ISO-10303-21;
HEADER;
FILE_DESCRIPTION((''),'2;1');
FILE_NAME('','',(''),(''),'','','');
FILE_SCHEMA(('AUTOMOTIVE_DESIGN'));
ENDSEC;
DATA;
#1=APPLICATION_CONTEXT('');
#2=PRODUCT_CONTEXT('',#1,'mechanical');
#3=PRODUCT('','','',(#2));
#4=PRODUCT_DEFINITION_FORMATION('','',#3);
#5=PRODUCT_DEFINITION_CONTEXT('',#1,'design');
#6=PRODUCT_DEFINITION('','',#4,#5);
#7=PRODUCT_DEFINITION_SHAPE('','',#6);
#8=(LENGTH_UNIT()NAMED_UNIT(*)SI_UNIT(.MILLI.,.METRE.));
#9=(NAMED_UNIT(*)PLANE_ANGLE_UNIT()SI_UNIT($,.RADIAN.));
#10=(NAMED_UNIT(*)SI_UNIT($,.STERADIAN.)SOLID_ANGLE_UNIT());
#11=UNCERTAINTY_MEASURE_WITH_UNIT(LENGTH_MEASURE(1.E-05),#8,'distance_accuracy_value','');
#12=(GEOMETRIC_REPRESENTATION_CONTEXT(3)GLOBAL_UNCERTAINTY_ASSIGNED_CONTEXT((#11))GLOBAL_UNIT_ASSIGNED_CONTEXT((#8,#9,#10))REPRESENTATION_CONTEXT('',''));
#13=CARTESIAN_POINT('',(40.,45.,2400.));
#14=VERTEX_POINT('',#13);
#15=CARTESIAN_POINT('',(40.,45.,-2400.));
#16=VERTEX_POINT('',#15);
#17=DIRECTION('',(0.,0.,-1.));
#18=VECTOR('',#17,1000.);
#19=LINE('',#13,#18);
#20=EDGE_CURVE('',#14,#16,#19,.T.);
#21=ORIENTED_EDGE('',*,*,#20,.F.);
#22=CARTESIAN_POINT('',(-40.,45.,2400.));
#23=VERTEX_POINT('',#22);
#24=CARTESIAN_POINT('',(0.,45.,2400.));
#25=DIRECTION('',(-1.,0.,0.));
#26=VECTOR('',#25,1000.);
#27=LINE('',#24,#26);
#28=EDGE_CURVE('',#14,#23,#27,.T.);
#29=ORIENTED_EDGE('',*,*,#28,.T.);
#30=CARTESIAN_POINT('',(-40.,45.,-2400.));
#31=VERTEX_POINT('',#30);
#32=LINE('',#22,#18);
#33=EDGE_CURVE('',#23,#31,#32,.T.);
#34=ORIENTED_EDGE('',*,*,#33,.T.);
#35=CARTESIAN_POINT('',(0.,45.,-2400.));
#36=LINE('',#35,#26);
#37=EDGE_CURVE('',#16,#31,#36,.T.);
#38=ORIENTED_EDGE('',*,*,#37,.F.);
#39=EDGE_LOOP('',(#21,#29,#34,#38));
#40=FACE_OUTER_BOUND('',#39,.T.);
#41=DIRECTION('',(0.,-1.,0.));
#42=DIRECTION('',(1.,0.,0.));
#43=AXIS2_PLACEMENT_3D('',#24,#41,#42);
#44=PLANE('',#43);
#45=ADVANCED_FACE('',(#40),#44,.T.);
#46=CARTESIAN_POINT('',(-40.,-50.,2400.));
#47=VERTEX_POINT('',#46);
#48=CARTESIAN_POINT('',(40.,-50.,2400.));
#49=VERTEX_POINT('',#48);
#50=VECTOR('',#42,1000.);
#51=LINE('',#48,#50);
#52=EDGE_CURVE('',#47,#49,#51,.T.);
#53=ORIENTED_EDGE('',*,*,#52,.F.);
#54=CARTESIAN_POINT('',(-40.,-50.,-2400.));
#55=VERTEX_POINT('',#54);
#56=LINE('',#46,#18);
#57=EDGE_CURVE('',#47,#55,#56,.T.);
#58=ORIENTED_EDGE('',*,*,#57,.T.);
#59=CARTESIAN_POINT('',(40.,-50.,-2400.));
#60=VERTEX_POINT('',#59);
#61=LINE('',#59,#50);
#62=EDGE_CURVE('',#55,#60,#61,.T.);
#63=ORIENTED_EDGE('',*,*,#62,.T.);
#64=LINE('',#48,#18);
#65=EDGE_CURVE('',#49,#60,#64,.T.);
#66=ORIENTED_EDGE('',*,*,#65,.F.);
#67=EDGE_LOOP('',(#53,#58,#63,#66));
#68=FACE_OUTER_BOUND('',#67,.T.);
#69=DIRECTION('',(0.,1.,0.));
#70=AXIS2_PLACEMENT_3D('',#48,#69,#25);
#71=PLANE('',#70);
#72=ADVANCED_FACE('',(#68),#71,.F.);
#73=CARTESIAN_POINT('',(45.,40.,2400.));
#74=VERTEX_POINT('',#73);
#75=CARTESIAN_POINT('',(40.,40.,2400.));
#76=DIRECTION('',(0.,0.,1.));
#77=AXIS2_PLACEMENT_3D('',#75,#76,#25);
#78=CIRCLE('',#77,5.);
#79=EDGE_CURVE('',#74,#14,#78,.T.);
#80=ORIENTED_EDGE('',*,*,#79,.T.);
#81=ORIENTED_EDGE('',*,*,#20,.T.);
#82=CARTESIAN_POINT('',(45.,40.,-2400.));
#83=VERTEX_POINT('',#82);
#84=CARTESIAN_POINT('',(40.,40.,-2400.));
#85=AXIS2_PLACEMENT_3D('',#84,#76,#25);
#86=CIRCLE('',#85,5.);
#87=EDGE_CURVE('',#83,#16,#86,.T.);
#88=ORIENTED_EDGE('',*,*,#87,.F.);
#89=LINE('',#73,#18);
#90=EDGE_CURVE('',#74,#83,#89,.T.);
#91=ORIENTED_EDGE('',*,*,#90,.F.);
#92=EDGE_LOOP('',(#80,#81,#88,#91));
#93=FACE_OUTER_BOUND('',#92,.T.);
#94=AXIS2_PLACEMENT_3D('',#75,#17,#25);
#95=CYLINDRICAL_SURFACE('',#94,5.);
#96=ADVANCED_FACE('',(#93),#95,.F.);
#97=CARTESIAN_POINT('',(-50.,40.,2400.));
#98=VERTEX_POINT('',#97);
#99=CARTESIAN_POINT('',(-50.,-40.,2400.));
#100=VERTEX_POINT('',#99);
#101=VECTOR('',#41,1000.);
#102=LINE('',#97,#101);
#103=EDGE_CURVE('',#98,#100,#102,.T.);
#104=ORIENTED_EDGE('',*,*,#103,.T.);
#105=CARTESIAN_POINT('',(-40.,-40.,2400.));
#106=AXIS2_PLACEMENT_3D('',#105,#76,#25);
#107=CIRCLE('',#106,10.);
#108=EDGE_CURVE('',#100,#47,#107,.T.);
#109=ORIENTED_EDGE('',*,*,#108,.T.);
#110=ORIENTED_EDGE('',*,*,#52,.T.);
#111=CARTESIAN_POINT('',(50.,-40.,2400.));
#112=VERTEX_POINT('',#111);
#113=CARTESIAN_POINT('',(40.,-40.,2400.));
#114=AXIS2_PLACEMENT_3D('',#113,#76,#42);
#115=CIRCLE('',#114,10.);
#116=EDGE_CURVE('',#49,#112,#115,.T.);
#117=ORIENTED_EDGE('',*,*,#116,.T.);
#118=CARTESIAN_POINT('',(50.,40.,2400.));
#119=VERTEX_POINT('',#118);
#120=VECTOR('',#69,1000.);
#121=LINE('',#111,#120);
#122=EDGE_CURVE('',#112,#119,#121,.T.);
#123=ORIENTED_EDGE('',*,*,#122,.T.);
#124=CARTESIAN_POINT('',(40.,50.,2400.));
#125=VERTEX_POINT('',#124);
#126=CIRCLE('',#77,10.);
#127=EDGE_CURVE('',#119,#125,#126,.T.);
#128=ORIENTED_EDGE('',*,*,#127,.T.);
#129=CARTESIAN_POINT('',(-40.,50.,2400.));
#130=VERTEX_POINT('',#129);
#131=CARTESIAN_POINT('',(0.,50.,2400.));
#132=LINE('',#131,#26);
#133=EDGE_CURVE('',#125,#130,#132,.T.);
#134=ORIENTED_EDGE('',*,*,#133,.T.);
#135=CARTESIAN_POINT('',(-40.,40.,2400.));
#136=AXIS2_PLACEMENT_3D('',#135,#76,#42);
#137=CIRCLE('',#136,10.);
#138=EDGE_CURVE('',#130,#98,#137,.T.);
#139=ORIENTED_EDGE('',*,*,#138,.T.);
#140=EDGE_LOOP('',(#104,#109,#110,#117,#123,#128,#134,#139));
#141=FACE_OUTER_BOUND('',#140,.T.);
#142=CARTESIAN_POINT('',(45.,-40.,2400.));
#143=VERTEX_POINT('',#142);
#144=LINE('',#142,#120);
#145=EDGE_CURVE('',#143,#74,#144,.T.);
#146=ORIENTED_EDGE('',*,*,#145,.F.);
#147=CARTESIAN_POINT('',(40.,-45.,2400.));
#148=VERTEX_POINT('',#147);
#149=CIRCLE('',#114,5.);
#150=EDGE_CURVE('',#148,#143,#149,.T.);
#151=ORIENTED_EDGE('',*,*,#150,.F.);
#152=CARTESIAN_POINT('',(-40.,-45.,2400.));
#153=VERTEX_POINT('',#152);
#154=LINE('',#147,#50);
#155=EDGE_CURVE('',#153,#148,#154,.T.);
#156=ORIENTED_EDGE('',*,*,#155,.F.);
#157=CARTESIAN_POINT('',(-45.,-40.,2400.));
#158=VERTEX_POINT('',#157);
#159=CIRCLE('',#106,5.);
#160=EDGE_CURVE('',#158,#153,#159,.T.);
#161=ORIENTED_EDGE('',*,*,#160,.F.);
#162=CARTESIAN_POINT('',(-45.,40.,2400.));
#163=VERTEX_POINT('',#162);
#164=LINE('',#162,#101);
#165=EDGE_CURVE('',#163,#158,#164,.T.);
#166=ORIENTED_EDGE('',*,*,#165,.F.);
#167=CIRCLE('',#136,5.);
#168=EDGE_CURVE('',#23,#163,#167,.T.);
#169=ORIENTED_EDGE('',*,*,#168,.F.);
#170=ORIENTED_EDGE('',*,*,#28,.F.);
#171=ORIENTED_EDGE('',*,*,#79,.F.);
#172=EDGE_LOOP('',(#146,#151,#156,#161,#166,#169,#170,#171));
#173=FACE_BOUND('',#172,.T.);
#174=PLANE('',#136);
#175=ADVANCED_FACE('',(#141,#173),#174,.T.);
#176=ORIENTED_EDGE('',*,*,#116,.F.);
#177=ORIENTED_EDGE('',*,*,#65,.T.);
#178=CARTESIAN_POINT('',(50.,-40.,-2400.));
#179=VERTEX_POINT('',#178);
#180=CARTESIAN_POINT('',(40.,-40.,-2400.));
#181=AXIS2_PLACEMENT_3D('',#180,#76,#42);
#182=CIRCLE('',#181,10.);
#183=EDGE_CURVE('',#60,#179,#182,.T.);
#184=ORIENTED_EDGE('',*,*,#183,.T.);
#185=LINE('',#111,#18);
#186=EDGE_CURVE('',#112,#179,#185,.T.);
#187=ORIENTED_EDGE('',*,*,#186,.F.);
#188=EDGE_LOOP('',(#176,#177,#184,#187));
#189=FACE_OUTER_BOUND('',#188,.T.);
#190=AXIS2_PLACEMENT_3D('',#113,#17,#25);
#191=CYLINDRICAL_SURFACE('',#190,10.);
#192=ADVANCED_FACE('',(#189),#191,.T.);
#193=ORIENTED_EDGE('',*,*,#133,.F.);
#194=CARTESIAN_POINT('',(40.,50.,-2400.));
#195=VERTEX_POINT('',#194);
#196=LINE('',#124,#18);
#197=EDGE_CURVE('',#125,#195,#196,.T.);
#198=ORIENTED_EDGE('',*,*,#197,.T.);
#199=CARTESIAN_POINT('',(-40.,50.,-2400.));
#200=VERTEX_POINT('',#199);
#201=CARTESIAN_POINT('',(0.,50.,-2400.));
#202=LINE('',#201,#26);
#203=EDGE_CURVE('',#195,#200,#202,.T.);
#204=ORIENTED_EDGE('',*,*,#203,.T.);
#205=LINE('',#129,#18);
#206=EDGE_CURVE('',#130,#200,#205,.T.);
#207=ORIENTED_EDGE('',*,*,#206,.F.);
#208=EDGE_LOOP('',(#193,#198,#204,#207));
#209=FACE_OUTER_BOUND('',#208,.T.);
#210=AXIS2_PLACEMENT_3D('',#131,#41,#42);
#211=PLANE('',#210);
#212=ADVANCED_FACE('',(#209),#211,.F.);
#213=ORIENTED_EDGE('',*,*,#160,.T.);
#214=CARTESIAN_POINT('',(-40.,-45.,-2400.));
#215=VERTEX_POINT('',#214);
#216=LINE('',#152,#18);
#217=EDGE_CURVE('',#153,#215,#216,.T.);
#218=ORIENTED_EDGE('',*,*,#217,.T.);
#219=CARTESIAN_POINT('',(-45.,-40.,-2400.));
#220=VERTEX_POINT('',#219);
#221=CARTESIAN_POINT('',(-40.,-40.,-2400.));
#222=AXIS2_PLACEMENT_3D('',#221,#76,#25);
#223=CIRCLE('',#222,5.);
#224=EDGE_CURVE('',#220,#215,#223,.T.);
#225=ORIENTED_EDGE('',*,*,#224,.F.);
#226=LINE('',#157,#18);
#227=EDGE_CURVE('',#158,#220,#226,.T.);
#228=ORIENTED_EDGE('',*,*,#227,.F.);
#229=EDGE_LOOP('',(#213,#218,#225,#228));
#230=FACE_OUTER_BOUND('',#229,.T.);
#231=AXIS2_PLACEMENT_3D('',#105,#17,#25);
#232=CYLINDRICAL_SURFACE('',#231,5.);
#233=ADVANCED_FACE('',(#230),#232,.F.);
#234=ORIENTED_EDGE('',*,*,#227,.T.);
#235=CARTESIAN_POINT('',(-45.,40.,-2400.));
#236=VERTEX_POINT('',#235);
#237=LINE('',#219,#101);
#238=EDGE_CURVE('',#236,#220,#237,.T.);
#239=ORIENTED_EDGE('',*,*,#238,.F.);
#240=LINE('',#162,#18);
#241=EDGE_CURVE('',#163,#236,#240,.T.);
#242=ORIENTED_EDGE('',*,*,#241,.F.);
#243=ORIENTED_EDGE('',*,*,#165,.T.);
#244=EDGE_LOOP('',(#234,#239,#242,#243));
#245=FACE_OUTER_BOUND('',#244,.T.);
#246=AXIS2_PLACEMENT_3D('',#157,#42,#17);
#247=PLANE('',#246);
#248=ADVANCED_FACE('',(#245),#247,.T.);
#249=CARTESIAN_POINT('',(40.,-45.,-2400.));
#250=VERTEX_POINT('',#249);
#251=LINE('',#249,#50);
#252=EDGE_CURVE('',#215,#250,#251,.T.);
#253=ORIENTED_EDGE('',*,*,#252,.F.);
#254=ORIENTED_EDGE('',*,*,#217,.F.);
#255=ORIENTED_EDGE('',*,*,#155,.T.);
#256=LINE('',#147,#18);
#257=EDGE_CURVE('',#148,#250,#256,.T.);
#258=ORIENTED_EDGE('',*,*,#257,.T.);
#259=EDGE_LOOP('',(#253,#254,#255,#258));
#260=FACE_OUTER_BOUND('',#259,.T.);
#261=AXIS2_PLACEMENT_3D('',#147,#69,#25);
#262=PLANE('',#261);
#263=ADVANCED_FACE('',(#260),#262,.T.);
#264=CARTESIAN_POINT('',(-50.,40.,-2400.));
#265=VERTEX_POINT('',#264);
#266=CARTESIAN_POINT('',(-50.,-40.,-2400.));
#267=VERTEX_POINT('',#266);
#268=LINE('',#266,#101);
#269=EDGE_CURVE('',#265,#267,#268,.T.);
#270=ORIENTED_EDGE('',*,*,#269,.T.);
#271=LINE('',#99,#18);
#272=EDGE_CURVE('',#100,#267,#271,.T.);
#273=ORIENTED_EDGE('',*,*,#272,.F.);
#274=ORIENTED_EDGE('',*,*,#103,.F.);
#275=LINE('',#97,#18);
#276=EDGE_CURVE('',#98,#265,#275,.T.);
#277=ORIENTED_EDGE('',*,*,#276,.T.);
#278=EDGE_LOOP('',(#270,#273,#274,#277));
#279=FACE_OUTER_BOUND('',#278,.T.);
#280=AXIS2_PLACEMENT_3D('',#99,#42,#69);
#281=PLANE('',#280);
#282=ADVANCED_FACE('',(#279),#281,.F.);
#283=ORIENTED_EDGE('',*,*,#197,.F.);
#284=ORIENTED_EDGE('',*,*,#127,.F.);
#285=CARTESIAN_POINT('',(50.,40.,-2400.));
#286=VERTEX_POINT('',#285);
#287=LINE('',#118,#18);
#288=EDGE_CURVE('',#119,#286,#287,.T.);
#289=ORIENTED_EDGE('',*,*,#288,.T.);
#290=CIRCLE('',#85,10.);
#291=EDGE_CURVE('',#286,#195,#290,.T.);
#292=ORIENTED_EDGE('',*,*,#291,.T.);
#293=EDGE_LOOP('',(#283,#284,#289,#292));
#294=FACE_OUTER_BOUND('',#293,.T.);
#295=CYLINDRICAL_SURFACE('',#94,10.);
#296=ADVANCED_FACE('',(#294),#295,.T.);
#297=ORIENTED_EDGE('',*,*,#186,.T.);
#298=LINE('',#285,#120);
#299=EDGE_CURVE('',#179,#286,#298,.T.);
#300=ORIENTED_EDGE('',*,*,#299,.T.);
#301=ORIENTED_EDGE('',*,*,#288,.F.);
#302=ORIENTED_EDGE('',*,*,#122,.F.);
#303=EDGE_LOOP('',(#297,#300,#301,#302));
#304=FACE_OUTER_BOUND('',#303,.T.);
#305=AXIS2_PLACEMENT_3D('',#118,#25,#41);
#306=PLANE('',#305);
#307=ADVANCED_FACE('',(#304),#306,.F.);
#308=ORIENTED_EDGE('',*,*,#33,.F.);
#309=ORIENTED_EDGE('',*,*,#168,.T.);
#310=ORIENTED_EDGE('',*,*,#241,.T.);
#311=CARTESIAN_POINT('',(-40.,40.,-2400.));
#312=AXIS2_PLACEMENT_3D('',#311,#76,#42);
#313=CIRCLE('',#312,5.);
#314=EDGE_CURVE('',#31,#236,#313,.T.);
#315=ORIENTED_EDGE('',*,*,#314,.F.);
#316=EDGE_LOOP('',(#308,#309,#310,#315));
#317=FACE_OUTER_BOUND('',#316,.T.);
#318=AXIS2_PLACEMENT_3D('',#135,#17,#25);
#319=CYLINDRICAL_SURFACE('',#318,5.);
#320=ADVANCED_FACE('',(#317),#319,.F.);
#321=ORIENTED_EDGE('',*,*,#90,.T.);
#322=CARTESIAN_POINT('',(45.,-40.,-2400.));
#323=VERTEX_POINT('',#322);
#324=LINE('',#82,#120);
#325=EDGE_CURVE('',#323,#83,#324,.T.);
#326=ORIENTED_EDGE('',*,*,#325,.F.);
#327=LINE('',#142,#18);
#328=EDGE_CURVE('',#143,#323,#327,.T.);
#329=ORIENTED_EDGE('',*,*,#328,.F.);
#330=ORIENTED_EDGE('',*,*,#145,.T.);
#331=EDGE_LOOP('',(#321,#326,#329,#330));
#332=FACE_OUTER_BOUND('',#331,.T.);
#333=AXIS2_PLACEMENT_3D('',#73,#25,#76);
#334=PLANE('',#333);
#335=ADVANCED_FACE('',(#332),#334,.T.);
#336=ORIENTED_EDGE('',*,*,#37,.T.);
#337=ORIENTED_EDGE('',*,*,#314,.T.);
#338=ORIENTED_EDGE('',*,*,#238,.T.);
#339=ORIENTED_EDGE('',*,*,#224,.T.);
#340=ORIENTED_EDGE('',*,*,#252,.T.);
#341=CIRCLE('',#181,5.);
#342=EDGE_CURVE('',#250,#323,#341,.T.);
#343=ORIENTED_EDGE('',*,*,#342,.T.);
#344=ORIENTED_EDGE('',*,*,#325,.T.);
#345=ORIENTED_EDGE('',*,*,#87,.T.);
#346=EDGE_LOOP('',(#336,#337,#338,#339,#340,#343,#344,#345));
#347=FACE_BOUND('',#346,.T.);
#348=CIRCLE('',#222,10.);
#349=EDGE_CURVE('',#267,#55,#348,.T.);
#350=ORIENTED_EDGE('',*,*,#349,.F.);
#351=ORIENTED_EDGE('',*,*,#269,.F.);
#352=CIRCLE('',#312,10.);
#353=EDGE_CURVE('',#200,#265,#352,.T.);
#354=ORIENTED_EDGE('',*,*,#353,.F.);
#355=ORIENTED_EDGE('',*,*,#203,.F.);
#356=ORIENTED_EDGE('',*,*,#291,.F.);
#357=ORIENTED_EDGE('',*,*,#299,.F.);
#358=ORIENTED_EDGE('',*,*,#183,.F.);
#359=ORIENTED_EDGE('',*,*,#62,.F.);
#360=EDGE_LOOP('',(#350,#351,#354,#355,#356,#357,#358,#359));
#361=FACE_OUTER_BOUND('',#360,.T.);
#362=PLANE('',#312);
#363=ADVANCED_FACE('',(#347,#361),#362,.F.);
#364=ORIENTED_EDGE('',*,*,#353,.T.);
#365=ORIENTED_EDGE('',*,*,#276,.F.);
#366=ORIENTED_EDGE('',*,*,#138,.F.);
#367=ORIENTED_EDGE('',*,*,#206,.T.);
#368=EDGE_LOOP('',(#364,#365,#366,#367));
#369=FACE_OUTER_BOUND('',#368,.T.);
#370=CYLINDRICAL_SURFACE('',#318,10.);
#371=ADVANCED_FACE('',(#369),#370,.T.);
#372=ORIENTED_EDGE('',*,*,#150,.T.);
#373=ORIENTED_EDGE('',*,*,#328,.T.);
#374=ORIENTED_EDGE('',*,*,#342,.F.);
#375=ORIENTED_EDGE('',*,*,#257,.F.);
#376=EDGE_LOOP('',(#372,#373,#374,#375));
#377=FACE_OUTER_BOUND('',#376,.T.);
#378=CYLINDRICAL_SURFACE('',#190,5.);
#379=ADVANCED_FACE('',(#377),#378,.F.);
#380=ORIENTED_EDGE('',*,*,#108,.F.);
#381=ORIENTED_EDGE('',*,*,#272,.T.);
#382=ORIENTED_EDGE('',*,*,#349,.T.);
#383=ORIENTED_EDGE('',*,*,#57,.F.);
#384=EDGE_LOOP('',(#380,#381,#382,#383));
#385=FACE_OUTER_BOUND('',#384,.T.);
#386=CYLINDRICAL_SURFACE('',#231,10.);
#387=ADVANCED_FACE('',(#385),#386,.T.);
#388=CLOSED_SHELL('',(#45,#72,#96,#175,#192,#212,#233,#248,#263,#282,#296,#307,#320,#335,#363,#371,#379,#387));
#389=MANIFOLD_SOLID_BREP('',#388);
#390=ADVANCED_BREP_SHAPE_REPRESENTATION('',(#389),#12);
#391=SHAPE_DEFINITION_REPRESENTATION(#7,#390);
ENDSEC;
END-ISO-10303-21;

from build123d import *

# Parameters (mm, degrees)
BOSS_EXTRUDE_1_DEPTH = 2400


with BuildPart() as part:
    # Sketch 1 → Boss-Extrude 1 (new, symmetric)
    with BuildSketch(Plane.XY):
        with BuildLine():
            Line((0, 50), (-40, 50))
            ThreePointArc((-40, 50), (-47.071067812, 47.071067812), (-50, 40))
            Line((-50, 40), (-50, 0))
            Line((-50, 0), (-50, -40))
            ThreePointArc((-50, -40), (-47.071067812, -47.071067812), (-40, -50))
            Line((-40, -50), (40, -50))
            ThreePointArc((40, -50), (47.071067812, -47.071067812), (50, -40))
            Line((50, -40), (50, 0))
            Line((50, 0), (50, 40))
            ThreePointArc((50, 40), (47.071067812, 47.071067812), (40, 50))
            Line((40, 50), (0, 50))
        make_face()
        with BuildLine():
            Line((0, 45), (-40, 45))
            ThreePointArc((-40, 45), (-43.535533906, 43.535533906), (-45, 40))
            Line((-45, 40), (-45, 0))
            Line((-45, 0), (-45, -40))
            ThreePointArc((-45, -40), (-43.535533906, -43.535533906), (-40, -45))
            Line((-40, -45), (40, -45))
            ThreePointArc((40, -45), (43.535533906, -43.535533906), (45, -40))
            Line((45, -40), (45, 0))
            Line((45, 0), (45, 40))
            ThreePointArc((45, 40), (43.535533906, 43.535533906), (40, 45))
            Line((40, 45), (0, 45))
        make_face(mode=Mode.SUBTRACT)
    extrude(amount=BOSS_EXTRUDE_1_DEPTH, both=True)


solid = part.part
